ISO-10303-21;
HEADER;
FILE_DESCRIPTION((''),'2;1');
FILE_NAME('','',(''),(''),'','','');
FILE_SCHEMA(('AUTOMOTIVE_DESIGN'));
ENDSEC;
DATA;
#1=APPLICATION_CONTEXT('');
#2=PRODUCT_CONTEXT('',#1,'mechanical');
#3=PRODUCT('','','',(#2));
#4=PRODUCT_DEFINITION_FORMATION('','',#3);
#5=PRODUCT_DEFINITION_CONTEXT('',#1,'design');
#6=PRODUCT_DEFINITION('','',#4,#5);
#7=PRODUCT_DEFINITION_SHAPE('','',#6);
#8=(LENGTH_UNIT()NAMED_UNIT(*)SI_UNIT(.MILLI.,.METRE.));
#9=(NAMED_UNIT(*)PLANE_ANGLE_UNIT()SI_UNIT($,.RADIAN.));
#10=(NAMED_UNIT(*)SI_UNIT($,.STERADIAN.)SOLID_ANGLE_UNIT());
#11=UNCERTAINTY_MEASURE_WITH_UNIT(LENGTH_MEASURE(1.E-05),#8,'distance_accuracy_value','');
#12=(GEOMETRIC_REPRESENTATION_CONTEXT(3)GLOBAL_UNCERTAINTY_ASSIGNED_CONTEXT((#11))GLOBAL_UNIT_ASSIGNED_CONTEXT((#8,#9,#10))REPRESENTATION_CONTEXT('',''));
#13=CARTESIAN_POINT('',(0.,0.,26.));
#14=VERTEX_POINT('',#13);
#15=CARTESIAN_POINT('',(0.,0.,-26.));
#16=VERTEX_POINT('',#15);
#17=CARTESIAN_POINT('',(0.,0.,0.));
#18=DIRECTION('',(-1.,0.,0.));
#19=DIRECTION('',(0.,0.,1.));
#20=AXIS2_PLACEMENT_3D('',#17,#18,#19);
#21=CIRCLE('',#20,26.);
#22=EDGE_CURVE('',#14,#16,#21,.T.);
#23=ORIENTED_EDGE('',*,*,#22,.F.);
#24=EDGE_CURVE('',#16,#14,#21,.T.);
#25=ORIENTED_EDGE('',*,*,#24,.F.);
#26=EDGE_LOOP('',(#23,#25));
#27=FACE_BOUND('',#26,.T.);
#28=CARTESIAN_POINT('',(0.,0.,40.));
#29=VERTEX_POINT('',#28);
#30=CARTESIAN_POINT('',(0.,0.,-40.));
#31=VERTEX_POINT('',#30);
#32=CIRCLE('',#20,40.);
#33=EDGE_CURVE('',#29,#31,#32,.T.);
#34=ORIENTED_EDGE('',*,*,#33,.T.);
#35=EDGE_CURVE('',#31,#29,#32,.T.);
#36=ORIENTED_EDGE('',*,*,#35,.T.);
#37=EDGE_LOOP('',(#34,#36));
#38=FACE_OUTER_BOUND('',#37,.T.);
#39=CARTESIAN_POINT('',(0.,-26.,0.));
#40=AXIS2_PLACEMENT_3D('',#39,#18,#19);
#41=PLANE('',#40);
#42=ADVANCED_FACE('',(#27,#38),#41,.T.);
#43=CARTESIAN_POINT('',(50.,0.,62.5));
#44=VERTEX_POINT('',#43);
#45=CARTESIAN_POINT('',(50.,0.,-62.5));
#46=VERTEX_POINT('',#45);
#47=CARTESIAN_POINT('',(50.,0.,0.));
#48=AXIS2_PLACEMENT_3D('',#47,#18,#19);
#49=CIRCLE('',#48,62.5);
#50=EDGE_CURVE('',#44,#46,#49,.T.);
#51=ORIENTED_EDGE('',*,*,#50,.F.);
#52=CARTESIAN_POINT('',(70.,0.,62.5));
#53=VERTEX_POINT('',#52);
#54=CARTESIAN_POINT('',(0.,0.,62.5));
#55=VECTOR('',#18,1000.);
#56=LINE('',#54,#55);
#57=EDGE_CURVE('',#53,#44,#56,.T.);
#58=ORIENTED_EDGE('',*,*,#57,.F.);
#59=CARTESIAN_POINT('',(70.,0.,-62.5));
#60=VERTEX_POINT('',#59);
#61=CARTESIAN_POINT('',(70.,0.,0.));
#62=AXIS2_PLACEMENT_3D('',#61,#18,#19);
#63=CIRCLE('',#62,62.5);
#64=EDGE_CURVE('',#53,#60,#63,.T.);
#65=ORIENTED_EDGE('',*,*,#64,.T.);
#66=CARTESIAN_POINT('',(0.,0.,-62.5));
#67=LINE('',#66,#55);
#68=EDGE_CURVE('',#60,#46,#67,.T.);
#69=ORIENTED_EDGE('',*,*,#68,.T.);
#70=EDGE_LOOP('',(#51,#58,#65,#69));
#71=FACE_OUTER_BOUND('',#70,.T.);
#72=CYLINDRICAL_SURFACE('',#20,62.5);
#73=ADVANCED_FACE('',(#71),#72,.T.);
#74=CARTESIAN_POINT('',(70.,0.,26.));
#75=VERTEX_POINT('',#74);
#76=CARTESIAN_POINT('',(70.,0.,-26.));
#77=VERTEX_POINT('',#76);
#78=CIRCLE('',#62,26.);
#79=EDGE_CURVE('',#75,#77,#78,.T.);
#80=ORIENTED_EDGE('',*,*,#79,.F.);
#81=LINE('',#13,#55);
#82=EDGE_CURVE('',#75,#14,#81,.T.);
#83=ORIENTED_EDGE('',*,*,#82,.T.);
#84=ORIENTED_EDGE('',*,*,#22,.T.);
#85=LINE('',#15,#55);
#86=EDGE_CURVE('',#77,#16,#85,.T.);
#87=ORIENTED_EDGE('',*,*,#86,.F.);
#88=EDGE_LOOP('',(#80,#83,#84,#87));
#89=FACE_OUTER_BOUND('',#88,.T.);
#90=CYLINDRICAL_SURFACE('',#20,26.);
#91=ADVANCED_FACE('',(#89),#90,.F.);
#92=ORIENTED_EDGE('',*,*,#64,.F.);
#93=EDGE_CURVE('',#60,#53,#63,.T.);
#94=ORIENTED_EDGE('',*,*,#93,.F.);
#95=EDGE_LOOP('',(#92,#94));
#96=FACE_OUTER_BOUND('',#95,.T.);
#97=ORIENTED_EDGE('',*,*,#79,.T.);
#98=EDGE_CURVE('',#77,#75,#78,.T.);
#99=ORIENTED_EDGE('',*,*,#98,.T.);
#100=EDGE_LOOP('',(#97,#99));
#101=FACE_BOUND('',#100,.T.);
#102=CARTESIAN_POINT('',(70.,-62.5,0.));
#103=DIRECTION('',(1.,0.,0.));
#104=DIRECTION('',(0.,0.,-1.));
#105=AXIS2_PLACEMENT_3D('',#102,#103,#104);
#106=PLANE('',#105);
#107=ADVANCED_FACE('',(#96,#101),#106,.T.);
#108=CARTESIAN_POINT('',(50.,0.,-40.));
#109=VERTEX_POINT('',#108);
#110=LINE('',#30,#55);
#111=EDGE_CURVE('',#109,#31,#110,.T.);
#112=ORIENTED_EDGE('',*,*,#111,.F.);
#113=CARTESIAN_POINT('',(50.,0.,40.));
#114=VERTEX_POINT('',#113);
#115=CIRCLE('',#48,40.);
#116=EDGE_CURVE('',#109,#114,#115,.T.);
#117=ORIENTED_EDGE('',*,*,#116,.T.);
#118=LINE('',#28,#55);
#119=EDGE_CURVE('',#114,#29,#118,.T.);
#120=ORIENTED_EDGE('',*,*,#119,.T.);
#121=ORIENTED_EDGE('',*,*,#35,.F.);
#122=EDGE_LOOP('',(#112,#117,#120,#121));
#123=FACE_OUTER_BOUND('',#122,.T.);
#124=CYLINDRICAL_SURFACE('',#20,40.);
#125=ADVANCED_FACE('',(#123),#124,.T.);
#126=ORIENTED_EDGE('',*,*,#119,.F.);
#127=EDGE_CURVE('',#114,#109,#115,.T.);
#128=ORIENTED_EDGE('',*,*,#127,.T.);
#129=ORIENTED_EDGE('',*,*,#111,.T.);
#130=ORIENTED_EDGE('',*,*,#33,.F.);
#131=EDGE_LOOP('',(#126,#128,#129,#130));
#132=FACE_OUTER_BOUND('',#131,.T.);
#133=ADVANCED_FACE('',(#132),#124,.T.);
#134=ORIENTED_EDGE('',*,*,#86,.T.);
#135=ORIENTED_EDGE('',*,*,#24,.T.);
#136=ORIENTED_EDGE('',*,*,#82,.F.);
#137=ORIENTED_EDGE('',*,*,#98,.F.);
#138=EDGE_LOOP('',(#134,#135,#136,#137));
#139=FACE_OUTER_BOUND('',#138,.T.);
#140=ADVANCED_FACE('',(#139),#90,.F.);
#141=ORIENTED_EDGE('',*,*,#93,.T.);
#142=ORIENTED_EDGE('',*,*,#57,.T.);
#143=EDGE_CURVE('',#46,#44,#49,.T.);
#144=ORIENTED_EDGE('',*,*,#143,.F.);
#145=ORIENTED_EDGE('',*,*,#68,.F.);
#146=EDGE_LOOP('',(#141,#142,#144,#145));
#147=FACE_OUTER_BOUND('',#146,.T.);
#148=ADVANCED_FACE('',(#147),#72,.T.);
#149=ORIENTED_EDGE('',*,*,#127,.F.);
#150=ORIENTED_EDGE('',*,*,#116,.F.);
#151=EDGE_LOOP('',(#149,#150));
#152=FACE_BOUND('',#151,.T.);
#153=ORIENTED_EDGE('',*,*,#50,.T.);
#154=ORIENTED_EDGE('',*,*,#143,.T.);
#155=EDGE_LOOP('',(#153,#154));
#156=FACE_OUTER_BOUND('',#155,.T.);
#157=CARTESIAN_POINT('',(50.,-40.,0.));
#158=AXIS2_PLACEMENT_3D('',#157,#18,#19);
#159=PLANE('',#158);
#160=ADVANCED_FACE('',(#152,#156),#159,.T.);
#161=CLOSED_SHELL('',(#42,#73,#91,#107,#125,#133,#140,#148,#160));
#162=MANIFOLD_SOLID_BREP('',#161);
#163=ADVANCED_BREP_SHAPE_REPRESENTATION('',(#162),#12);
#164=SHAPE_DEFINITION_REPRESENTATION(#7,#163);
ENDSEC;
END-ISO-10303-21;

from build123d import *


with BuildPart() as part:
    # Sketch1 → Revolve1 (revolve)
    with BuildSketch(Plane.XY, mode=Mode.PRIVATE) as revolve1_sk:
        Polygon((0, -26), (0, -40), (50, -40), (50, -62.5), (70, -62.5), (70, -26), align=None)
    revolve(revolve1_sk.sketch.rotate(Axis((0, 0, 0), (1, 0, 0)), 270), axis=Axis((0, 0, 0), (1, 0, 0)))


solid = part.part
